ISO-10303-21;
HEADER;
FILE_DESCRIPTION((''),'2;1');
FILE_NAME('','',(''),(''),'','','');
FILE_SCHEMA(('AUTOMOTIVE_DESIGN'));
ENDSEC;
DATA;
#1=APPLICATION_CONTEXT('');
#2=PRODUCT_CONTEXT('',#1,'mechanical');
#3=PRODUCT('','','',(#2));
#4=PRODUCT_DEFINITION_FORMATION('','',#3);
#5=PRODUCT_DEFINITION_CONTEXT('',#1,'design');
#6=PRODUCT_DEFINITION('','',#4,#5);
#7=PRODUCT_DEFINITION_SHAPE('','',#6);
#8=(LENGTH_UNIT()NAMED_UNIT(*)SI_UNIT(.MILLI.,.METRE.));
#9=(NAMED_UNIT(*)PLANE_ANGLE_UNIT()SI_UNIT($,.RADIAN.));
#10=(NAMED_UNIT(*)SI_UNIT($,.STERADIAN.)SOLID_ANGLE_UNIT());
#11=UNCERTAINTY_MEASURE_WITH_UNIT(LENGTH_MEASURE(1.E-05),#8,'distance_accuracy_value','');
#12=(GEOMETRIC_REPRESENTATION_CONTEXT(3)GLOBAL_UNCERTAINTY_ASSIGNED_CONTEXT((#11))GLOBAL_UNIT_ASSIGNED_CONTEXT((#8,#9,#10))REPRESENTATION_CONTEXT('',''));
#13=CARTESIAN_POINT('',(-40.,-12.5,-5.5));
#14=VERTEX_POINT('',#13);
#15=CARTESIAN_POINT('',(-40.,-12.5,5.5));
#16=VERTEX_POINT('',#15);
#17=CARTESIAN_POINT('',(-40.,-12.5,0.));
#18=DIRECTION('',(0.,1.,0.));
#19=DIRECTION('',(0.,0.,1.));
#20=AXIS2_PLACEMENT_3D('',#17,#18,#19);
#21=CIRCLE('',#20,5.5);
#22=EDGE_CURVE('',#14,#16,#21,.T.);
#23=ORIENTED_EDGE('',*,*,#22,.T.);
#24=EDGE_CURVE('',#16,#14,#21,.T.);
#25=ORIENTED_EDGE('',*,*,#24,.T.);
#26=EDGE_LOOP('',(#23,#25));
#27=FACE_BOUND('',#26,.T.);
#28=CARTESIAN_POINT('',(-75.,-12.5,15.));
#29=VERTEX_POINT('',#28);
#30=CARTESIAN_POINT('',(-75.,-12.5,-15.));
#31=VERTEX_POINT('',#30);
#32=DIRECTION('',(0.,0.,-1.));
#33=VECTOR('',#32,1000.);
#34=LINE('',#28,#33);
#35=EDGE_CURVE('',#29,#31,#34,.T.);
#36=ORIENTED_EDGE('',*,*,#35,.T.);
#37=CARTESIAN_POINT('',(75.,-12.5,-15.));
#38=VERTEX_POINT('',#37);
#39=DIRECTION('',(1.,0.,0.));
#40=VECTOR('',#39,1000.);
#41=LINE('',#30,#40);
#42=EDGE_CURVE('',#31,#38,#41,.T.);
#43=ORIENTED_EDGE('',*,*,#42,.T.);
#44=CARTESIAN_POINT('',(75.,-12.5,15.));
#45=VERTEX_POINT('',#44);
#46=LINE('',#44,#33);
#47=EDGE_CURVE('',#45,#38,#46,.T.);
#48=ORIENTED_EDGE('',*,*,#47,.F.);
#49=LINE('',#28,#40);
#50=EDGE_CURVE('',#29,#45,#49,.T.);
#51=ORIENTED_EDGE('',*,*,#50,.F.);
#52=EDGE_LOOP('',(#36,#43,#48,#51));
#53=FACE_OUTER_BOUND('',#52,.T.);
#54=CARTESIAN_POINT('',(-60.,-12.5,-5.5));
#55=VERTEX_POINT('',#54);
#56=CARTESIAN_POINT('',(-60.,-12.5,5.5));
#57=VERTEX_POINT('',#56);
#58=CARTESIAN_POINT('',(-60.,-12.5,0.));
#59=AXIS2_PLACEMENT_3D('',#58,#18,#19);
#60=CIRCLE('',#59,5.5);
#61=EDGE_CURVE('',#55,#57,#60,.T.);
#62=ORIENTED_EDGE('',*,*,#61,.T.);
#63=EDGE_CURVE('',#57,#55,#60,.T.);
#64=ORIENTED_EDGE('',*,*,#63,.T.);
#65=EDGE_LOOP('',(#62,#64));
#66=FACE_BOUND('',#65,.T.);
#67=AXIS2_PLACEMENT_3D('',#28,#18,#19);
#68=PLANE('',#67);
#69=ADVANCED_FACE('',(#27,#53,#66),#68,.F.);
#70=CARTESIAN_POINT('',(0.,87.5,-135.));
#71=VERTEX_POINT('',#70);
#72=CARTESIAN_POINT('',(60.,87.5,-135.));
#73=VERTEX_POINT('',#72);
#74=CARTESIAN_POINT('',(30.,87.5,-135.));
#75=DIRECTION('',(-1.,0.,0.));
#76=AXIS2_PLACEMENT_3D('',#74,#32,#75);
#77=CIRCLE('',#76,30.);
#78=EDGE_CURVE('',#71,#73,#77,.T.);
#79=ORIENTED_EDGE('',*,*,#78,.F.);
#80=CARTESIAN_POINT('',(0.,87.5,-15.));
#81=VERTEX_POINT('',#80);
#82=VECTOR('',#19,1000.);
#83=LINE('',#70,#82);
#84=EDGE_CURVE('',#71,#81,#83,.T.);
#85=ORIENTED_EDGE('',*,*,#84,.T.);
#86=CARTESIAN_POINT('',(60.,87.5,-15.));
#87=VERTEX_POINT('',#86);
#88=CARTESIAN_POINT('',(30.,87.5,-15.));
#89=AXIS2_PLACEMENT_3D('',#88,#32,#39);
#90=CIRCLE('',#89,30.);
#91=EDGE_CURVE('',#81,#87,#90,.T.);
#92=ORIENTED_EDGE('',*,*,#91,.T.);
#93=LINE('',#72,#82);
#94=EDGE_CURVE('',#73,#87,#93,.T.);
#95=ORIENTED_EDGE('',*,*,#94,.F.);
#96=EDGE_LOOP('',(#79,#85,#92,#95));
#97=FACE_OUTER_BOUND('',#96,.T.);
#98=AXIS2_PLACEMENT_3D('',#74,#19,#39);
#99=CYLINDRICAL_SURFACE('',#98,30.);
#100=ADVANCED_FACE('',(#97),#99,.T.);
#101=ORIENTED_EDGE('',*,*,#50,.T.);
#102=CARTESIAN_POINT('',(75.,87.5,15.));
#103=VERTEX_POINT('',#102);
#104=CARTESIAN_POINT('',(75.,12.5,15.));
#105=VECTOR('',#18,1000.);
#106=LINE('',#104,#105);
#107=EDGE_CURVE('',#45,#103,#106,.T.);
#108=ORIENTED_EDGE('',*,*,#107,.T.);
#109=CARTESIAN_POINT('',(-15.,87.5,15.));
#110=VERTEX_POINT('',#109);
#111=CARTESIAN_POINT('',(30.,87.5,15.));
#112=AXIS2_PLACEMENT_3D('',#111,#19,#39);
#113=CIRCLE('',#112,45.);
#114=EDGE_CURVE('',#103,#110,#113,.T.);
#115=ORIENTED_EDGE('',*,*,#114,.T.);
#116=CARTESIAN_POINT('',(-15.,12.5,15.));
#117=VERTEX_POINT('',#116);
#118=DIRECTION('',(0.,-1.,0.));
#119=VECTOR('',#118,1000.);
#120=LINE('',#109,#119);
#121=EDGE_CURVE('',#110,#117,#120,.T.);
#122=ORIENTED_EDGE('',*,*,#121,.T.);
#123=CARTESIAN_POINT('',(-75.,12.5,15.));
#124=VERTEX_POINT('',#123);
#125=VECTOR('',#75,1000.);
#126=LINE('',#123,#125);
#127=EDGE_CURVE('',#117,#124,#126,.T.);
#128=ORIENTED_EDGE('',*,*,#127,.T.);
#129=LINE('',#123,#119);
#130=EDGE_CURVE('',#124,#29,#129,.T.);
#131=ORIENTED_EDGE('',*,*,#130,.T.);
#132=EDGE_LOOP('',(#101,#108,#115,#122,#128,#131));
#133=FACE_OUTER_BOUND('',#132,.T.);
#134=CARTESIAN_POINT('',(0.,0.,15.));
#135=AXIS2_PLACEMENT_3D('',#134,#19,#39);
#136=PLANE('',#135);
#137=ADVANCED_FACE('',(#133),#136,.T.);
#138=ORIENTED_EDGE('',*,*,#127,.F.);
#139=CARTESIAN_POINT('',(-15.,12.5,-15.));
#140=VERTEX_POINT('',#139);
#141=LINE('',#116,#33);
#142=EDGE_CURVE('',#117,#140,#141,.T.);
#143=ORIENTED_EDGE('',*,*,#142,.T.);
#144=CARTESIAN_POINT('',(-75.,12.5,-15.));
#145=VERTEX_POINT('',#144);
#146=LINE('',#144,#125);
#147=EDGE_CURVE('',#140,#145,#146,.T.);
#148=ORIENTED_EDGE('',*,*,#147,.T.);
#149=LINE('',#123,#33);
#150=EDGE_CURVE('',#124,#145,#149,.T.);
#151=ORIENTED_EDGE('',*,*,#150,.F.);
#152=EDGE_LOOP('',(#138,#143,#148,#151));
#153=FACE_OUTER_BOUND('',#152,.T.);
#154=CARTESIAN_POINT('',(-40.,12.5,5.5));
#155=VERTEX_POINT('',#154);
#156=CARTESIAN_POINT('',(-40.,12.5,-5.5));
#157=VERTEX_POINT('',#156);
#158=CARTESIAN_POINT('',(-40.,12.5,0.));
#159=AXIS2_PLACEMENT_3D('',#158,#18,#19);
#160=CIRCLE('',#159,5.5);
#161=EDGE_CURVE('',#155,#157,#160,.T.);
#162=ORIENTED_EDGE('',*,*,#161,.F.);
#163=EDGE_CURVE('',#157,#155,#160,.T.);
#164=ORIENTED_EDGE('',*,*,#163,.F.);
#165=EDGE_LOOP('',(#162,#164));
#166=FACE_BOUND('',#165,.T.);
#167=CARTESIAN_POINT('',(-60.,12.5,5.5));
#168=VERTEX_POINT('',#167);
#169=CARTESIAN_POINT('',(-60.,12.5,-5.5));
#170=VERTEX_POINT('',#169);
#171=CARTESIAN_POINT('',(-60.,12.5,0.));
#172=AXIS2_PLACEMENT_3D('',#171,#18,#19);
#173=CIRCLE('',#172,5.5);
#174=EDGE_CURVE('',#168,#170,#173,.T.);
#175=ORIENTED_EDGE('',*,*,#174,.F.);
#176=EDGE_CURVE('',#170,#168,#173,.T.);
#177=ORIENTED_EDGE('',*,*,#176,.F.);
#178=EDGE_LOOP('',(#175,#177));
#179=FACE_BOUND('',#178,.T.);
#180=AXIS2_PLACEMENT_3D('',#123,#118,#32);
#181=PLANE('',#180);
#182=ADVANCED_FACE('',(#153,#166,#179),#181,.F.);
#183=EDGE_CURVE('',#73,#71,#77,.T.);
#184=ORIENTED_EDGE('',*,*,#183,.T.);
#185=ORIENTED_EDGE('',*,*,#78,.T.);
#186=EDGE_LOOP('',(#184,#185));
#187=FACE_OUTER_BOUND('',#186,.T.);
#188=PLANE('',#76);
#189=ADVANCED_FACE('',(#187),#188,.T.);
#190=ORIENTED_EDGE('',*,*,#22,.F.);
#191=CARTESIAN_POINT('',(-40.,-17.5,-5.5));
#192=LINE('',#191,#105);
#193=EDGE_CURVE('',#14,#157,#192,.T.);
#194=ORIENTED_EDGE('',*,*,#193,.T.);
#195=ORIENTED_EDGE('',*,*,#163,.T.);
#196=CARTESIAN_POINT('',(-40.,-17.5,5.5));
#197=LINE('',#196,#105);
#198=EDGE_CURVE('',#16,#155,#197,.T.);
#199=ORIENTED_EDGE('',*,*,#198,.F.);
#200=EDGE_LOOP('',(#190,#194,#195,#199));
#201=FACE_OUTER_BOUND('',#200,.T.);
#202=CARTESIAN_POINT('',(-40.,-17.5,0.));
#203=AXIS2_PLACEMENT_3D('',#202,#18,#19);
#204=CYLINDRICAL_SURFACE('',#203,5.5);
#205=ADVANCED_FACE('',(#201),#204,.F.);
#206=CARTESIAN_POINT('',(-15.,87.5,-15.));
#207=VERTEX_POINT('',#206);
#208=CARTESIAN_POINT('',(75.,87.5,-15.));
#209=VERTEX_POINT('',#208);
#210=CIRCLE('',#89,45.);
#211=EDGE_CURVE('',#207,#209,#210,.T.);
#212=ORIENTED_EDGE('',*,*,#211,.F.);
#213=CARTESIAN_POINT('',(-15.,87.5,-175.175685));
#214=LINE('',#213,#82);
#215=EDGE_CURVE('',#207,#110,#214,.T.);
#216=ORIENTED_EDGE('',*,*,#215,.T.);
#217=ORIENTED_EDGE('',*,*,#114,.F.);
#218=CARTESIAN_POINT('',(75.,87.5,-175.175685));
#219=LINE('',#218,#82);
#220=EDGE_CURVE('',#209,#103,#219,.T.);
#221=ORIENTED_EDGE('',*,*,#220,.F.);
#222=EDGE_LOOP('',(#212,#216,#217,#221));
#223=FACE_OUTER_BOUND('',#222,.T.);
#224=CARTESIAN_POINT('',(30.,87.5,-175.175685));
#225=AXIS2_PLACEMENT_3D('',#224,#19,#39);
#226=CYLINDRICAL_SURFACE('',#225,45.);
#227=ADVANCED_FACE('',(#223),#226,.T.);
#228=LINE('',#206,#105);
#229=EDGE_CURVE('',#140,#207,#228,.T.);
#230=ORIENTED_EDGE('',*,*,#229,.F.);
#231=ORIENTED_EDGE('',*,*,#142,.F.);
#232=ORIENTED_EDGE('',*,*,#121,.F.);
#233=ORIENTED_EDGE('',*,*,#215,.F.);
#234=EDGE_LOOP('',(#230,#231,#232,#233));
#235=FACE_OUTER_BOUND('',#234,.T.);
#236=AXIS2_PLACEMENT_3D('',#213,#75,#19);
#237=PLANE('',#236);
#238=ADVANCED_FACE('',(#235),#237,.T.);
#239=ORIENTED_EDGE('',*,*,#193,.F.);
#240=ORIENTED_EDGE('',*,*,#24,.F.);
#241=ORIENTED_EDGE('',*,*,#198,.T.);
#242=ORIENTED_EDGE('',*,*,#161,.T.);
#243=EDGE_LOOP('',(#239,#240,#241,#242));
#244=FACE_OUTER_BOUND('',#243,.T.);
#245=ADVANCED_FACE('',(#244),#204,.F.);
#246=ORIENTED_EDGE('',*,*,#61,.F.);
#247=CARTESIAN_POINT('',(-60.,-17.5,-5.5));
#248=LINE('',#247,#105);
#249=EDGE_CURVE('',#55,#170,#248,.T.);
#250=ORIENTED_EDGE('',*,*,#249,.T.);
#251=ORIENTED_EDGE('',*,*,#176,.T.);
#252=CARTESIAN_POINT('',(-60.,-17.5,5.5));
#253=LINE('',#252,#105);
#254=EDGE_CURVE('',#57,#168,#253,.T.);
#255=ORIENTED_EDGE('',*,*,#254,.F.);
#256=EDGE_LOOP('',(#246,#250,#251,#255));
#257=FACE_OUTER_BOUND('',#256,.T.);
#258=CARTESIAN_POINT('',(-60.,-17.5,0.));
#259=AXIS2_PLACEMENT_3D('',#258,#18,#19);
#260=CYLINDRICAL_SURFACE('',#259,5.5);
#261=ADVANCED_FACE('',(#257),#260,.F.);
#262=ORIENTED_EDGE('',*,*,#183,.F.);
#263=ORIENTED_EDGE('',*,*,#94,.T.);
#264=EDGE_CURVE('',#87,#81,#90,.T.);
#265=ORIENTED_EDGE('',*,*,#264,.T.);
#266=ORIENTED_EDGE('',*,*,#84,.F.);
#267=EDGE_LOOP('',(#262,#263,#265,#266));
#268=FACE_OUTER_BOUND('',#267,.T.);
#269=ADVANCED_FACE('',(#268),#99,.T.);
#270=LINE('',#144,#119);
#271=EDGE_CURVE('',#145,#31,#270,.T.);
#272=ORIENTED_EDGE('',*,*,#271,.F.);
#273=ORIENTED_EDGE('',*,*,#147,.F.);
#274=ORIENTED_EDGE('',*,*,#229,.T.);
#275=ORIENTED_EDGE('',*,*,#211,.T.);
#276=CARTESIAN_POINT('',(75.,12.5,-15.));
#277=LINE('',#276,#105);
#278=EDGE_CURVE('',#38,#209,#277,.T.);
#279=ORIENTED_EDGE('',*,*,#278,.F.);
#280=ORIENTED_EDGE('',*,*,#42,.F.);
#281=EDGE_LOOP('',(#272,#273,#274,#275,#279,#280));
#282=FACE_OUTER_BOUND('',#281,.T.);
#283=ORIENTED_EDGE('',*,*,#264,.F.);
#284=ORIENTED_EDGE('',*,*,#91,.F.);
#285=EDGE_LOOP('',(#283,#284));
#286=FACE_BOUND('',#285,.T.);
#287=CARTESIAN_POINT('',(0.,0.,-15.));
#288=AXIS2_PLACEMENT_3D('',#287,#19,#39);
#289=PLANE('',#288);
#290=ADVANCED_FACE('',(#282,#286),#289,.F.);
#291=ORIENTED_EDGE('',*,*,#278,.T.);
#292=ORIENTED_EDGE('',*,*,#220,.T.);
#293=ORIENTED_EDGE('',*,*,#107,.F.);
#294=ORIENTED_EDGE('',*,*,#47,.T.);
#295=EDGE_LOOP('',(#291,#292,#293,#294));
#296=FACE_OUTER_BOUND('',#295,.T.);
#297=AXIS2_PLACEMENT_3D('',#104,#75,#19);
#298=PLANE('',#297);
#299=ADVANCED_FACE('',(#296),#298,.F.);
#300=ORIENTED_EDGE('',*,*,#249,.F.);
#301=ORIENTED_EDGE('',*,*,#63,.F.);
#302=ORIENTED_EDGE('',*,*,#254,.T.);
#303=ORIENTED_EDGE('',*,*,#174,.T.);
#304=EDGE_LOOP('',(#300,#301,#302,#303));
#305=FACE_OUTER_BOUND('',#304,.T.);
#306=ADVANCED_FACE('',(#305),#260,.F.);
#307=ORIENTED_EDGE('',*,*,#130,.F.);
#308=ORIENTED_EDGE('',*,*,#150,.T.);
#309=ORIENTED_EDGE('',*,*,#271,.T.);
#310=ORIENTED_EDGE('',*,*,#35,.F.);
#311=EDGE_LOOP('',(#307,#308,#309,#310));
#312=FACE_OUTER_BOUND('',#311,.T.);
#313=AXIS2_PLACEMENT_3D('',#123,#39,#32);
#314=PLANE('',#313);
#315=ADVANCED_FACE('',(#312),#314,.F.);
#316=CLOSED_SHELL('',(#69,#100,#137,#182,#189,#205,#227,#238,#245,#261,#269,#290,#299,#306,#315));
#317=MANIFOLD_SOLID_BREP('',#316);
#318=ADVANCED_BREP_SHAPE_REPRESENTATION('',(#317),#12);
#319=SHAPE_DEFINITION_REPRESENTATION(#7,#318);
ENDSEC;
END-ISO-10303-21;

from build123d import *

# Parameters (mm, degrees)
SKETCH2_W           = 150
SKETCH2_H           = 25
BOSS_EXTRUDE1_DEPTH = 15
SKETCH3_R           = 30
BOSS_EXTRUDE2_DEPTH = 30
SKETCH4_R           = 5.5
CUT_EXTRUDE1_DEPTH  = 30
BOSS_EXTRUDE3_START = -30
SKETCH5_R           = 30
BOSS_EXTRUDE3_DEPTH = 150


with BuildPart() as part:
    # Sketch2 → Boss-Extrude1 (new, symmetric)
    with BuildSketch(Plane.XY):
        Rectangle(SKETCH2_W, SKETCH2_H)
    extrude(amount=BOSS_EXTRUDE1_DEPTH, both=True)

    # Sketch3 → Boss-Extrude2 (add)
    with BuildSketch(Plane.XY.offset(15)):
        with BuildLine():
            Line((-15, 87.5), (-15, 0))
            Line((-15, 0), (75, 0))
            Line((75, 0), (75, 87.5))
            ThreePointArc((75, 87.5), (30, 132.5), (-15, 87.5))
        make_face()
        with Locations((30, 87.5)):
            Circle(SKETCH3_R, mode=Mode.SUBTRACT)
    extrude(amount=-BOSS_EXTRUDE2_DEPTH)

    # Sketch4 → Cut-Extrude1 (cut)
    with BuildSketch(Plane(origin=(0, 12.5, 0), x_dir=(1, 0, 0), z_dir=(0, 1, 0))):
        with Locations(Location((-60, 0, 0), (0, 0, 270))):
            Circle(SKETCH4_R)
        with Locations(Location((-40, 0, 0), (0, 0, 270))):
            Circle(SKETCH4_R)
    extrude(amount=-CUT_EXTRUDE1_DEPTH, mode=Mode.SUBTRACT)

    # Sketch5 → Boss-Extrude3 (add)
    with BuildSketch(Plane(origin=(0, 0, -15), x_dir=(-1, 0, 0), z_dir=(0, 0, -1)).offset(BOSS_EXTRUDE3_START)):
        with Locations(Location((-30, 87.5, 0), (0, 0, 180))):
            Circle(SKETCH5_R)
    extrude(amount=BOSS_EXTRUDE3_DEPTH)


solid = part.part
